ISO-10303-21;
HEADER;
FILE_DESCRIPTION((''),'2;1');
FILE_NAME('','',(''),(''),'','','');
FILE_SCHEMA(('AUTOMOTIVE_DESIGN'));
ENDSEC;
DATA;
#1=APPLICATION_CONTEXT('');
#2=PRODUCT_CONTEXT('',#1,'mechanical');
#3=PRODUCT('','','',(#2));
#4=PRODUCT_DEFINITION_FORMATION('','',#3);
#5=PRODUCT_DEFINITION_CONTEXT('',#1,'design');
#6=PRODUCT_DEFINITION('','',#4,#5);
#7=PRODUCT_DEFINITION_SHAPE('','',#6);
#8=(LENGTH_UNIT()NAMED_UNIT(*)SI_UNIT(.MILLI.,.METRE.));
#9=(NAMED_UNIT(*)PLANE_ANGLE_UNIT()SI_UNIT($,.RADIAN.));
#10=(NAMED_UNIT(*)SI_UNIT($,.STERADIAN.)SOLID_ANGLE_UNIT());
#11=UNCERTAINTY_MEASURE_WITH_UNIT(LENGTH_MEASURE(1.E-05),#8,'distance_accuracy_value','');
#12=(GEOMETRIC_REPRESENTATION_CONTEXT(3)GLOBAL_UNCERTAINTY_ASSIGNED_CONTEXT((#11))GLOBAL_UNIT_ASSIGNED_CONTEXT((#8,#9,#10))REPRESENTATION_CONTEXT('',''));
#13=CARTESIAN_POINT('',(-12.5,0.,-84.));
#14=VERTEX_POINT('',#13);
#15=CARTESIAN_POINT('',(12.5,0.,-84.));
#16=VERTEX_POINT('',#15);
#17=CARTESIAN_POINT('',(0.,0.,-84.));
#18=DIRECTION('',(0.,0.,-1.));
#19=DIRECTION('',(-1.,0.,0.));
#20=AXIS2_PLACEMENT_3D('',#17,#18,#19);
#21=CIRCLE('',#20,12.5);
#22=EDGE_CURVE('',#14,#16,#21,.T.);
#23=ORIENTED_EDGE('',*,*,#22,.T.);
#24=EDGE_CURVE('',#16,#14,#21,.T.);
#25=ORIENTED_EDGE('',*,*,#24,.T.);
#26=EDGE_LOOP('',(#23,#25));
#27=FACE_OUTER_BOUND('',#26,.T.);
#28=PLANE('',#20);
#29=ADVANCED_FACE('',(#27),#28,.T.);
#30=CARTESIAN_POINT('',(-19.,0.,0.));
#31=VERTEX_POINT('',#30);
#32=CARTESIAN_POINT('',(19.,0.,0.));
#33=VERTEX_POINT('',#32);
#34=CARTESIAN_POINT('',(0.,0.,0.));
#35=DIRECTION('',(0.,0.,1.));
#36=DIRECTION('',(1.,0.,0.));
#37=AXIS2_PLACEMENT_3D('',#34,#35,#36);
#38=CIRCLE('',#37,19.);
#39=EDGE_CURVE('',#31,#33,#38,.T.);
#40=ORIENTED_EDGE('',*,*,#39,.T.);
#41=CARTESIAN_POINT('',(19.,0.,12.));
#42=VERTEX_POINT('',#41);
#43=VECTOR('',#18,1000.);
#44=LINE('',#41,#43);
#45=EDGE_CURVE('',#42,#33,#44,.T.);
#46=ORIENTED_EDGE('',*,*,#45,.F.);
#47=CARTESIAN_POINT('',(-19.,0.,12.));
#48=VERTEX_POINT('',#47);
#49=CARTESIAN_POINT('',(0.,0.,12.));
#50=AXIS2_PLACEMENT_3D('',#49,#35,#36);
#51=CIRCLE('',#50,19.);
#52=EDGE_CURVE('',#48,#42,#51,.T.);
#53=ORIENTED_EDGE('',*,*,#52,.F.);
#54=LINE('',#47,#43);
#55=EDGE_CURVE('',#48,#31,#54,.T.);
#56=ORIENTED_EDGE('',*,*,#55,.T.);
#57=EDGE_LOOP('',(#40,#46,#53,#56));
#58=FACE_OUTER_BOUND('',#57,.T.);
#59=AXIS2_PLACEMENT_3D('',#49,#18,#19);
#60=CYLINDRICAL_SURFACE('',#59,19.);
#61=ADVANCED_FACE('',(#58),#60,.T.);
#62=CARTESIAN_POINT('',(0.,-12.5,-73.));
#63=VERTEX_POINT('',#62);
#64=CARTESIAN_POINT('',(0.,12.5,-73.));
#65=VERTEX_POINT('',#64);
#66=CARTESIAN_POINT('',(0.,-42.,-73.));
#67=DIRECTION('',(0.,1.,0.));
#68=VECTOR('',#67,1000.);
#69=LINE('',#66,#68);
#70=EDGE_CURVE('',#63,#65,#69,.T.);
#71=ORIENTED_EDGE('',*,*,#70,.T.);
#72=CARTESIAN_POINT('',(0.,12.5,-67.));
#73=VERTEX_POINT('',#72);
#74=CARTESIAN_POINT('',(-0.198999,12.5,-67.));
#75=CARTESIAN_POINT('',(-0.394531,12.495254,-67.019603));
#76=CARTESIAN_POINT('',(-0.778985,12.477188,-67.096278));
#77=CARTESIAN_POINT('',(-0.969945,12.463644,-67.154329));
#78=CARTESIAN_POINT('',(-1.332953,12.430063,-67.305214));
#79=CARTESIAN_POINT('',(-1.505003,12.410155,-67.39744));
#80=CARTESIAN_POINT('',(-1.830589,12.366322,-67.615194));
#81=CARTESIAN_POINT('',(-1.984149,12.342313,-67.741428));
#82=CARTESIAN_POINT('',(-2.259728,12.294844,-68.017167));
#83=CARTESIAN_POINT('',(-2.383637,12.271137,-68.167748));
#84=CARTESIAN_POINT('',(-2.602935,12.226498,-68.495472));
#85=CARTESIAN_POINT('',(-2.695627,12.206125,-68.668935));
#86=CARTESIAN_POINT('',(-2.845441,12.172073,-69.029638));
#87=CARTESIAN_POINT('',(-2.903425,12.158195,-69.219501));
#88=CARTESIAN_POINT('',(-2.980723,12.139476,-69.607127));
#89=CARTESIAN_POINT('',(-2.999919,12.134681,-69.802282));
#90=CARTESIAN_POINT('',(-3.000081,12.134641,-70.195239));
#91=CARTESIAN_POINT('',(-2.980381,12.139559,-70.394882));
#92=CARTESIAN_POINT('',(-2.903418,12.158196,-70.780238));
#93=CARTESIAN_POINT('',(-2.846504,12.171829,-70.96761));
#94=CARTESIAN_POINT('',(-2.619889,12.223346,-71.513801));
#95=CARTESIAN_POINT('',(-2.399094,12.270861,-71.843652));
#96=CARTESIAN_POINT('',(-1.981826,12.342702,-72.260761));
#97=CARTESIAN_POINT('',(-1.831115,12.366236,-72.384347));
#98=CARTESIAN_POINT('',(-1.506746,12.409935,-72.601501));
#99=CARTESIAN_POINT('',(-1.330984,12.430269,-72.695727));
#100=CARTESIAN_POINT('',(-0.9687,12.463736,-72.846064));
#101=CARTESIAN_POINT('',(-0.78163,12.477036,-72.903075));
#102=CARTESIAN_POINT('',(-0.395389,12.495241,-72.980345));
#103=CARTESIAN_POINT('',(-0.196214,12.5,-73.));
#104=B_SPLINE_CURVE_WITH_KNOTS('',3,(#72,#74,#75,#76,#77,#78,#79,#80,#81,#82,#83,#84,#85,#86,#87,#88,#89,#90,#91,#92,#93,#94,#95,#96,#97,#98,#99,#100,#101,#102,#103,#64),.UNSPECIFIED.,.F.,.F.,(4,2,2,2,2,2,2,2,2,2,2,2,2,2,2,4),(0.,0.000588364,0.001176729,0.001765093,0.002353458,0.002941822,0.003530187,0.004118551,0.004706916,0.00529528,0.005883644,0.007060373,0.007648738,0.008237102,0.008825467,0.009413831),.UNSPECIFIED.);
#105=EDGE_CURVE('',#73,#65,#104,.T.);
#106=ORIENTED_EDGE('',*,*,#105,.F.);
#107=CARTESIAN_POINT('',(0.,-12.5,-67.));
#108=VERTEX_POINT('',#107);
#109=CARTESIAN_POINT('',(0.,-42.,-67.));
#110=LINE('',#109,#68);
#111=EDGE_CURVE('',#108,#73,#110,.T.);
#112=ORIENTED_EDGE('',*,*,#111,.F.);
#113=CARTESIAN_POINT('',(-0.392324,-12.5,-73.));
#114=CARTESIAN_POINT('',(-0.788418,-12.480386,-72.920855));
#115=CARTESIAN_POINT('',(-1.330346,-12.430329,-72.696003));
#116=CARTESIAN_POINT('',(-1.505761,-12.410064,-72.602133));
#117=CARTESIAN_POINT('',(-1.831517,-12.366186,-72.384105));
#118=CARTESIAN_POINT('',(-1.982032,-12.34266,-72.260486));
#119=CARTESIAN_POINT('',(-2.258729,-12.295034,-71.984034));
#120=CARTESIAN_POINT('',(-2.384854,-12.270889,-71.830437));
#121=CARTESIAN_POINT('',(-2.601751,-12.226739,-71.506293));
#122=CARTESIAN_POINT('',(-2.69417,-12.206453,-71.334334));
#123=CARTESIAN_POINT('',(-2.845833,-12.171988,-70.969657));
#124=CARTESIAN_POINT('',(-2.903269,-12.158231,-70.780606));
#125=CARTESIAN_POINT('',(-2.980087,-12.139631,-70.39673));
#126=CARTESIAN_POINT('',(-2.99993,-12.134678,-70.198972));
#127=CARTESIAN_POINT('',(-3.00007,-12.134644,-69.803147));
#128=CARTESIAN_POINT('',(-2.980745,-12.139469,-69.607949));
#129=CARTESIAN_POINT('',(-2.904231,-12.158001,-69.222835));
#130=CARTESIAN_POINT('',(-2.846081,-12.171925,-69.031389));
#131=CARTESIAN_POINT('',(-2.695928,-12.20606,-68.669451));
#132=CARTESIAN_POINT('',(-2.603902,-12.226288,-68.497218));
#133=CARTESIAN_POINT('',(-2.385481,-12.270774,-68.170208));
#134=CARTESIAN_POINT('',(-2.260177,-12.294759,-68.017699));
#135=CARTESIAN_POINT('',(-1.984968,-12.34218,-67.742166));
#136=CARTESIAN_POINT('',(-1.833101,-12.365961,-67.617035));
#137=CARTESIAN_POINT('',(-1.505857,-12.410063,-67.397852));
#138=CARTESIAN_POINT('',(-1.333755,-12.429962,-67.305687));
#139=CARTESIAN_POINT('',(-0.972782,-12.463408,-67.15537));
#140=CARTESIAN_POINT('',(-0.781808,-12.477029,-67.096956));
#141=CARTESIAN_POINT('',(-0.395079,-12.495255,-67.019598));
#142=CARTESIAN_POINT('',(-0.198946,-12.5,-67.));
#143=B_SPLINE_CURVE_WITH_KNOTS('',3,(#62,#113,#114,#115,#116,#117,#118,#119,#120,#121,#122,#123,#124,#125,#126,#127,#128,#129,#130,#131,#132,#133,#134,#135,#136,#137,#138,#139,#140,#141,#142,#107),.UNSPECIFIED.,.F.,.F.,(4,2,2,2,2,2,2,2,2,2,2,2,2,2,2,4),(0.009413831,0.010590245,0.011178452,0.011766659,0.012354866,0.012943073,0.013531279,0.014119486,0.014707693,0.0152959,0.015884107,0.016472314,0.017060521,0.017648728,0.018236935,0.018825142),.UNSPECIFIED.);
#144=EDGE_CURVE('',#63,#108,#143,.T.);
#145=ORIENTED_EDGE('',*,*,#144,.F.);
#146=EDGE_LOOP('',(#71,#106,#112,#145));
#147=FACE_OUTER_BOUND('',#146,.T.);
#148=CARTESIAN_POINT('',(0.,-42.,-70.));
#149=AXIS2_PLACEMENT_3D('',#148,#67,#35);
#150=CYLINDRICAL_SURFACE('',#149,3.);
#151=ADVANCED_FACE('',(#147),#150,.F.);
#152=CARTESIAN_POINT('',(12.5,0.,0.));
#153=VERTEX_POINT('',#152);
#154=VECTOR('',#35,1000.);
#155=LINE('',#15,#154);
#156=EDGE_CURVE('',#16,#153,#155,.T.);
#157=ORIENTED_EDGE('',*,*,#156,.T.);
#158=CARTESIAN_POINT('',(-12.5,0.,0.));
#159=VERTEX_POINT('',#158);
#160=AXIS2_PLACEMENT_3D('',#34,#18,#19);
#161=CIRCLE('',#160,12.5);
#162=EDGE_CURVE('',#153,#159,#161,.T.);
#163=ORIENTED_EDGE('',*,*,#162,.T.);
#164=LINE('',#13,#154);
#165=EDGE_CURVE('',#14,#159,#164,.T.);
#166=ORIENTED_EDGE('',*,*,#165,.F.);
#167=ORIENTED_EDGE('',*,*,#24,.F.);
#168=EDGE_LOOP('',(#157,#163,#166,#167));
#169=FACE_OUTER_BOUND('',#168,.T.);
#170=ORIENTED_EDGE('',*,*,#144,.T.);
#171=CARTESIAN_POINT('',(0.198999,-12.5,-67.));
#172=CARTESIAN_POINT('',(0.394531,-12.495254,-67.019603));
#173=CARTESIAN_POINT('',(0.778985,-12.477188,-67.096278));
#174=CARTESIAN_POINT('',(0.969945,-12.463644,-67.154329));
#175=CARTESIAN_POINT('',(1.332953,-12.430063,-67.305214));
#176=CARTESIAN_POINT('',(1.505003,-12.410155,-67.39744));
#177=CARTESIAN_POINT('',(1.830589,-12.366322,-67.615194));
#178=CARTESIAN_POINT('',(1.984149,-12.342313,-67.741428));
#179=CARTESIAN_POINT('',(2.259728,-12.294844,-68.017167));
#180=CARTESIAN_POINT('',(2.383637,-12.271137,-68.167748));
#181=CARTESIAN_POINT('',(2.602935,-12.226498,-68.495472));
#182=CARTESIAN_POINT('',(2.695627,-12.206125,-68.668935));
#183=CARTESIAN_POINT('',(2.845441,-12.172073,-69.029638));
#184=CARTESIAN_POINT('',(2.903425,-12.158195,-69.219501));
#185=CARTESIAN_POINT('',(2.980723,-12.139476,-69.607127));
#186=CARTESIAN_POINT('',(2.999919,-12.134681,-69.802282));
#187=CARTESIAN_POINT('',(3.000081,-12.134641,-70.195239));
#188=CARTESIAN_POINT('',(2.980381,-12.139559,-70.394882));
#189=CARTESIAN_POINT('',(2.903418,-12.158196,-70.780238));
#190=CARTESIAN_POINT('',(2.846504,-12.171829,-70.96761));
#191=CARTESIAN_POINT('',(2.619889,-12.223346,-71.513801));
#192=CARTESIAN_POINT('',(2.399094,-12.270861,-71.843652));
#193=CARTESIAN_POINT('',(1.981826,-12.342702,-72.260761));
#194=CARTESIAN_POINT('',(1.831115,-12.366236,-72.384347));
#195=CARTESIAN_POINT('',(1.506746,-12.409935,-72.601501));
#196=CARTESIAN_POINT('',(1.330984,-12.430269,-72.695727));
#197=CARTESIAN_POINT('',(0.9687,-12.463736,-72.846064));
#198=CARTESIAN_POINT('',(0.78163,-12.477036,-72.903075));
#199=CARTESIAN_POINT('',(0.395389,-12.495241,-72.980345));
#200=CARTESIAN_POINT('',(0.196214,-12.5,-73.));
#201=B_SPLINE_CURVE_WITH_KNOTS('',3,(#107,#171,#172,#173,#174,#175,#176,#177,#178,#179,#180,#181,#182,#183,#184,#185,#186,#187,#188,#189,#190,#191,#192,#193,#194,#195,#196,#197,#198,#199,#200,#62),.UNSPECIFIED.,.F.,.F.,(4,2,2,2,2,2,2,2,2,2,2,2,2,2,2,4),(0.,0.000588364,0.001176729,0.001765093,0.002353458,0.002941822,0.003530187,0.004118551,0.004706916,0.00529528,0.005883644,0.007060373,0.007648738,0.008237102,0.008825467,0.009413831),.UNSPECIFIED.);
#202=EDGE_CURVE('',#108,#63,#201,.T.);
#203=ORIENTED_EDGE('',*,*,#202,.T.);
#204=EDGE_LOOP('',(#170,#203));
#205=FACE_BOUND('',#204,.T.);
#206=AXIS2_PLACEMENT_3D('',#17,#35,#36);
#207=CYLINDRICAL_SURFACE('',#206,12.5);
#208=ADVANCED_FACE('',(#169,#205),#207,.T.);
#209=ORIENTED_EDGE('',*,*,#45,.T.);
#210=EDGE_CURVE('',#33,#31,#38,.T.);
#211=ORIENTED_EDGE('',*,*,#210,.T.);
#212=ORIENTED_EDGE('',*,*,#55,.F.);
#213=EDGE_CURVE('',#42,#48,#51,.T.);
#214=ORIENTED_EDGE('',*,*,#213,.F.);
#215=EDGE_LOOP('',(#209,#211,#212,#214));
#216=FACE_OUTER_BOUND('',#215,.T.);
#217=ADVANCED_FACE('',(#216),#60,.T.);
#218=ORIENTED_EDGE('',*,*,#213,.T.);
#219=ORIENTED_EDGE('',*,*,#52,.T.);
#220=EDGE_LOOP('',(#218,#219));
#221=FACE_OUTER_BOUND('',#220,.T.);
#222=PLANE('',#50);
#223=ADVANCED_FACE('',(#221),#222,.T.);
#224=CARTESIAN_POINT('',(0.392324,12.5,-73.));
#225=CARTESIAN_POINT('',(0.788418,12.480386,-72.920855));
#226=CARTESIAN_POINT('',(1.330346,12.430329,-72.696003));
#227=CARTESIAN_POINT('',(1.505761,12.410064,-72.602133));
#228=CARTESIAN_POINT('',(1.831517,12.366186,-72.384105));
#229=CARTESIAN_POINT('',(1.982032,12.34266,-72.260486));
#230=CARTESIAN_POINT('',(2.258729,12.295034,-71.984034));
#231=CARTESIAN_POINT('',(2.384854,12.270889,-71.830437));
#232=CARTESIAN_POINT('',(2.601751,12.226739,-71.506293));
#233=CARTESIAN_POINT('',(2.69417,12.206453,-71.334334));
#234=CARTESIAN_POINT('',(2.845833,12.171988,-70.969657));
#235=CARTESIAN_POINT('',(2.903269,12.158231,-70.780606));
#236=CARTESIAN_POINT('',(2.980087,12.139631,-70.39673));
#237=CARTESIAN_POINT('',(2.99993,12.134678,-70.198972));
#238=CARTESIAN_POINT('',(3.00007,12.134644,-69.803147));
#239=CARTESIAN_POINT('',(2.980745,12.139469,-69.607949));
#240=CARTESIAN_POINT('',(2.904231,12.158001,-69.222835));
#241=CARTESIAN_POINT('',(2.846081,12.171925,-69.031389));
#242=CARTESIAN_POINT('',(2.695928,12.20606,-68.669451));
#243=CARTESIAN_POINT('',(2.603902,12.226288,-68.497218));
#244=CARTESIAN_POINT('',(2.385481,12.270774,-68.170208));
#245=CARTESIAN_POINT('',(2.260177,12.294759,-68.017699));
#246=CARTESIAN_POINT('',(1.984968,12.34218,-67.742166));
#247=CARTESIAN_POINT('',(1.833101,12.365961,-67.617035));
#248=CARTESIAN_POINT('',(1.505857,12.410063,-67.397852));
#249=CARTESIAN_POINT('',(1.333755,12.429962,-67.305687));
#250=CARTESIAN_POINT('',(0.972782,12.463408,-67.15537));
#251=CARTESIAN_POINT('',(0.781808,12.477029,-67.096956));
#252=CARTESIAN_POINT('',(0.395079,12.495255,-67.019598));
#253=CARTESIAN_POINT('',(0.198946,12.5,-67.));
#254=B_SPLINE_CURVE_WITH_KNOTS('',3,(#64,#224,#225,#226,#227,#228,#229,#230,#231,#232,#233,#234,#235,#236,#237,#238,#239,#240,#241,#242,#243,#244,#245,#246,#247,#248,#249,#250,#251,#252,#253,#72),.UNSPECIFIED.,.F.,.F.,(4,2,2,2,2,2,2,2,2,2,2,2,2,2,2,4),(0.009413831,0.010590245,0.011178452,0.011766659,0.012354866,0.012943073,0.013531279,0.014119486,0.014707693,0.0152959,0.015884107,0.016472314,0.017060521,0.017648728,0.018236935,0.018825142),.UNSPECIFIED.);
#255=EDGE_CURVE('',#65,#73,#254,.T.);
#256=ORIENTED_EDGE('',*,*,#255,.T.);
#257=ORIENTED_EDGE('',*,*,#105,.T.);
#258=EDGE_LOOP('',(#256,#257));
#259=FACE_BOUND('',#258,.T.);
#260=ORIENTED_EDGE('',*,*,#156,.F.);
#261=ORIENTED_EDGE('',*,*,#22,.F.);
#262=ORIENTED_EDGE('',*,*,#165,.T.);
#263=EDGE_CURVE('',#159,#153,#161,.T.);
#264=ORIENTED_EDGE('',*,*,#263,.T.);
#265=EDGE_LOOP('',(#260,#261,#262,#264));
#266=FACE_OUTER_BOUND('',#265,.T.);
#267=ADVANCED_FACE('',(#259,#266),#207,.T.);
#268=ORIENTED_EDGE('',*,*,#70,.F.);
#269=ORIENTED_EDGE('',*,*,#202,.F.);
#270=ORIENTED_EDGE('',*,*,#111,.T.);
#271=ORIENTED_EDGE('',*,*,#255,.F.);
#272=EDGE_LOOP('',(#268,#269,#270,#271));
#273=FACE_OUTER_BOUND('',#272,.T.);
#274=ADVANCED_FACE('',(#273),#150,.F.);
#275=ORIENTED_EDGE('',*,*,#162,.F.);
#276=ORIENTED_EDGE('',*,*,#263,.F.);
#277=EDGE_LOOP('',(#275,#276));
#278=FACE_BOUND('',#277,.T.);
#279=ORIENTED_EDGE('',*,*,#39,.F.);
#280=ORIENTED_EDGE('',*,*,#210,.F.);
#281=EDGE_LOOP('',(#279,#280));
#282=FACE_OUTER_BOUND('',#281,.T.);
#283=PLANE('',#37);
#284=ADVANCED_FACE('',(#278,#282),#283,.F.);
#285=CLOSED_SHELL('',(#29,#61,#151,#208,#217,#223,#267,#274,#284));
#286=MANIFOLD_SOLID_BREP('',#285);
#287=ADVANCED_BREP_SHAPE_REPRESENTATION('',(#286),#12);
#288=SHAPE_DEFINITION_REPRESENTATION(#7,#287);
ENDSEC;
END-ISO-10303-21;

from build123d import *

# Parameters (mm, degrees)
HEAD_PROFILE_38_R      = 19
HEAD_38X12_DEPTH       = 12
SHANK_PROFILE_25_R     = 12.5
SHANK_25X84_DEPTH      = 84
CROSS_HOLE_PROFILE_6_R = 3
CROSS_HOLE_6_DEPTH     = 42


with BuildPart() as part:
    # Head Profile Ø38 → Head Ø38x12 (new body)
    with BuildSketch(Plane.XY):
        Circle(HEAD_PROFILE_38_R)
    extrude(amount=HEAD_38X12_DEPTH)

    # Shank Profile Ø25 → Shank Ø25x84 (add)
    with BuildSketch(Plane(origin=(0, 0, 0), x_dir=(-1, 0, 0), z_dir=(0, 0, -1))):
        with Locations(Location((0, 0, 0), (0, 0, 180))):
            Circle(SHANK_PROFILE_25_R)
    extrude(amount=SHANK_25X84_DEPTH)

    # Cross Hole Profile Ø6 → Cross Hole Ø6 (cut, symmetric)
    with BuildSketch(Plane(origin=(0, 0, 0), x_dir=(1, 0, 0), z_dir=(0, 1, 0))):
        with Locations(Location((0, 70, 0), (0, 0, 270))):
            Circle(CROSS_HOLE_PROFILE_6_R)
    extrude(amount=CROSS_HOLE_6_DEPTH, both=True, mode=Mode.SUBTRACT)


solid = part.part
